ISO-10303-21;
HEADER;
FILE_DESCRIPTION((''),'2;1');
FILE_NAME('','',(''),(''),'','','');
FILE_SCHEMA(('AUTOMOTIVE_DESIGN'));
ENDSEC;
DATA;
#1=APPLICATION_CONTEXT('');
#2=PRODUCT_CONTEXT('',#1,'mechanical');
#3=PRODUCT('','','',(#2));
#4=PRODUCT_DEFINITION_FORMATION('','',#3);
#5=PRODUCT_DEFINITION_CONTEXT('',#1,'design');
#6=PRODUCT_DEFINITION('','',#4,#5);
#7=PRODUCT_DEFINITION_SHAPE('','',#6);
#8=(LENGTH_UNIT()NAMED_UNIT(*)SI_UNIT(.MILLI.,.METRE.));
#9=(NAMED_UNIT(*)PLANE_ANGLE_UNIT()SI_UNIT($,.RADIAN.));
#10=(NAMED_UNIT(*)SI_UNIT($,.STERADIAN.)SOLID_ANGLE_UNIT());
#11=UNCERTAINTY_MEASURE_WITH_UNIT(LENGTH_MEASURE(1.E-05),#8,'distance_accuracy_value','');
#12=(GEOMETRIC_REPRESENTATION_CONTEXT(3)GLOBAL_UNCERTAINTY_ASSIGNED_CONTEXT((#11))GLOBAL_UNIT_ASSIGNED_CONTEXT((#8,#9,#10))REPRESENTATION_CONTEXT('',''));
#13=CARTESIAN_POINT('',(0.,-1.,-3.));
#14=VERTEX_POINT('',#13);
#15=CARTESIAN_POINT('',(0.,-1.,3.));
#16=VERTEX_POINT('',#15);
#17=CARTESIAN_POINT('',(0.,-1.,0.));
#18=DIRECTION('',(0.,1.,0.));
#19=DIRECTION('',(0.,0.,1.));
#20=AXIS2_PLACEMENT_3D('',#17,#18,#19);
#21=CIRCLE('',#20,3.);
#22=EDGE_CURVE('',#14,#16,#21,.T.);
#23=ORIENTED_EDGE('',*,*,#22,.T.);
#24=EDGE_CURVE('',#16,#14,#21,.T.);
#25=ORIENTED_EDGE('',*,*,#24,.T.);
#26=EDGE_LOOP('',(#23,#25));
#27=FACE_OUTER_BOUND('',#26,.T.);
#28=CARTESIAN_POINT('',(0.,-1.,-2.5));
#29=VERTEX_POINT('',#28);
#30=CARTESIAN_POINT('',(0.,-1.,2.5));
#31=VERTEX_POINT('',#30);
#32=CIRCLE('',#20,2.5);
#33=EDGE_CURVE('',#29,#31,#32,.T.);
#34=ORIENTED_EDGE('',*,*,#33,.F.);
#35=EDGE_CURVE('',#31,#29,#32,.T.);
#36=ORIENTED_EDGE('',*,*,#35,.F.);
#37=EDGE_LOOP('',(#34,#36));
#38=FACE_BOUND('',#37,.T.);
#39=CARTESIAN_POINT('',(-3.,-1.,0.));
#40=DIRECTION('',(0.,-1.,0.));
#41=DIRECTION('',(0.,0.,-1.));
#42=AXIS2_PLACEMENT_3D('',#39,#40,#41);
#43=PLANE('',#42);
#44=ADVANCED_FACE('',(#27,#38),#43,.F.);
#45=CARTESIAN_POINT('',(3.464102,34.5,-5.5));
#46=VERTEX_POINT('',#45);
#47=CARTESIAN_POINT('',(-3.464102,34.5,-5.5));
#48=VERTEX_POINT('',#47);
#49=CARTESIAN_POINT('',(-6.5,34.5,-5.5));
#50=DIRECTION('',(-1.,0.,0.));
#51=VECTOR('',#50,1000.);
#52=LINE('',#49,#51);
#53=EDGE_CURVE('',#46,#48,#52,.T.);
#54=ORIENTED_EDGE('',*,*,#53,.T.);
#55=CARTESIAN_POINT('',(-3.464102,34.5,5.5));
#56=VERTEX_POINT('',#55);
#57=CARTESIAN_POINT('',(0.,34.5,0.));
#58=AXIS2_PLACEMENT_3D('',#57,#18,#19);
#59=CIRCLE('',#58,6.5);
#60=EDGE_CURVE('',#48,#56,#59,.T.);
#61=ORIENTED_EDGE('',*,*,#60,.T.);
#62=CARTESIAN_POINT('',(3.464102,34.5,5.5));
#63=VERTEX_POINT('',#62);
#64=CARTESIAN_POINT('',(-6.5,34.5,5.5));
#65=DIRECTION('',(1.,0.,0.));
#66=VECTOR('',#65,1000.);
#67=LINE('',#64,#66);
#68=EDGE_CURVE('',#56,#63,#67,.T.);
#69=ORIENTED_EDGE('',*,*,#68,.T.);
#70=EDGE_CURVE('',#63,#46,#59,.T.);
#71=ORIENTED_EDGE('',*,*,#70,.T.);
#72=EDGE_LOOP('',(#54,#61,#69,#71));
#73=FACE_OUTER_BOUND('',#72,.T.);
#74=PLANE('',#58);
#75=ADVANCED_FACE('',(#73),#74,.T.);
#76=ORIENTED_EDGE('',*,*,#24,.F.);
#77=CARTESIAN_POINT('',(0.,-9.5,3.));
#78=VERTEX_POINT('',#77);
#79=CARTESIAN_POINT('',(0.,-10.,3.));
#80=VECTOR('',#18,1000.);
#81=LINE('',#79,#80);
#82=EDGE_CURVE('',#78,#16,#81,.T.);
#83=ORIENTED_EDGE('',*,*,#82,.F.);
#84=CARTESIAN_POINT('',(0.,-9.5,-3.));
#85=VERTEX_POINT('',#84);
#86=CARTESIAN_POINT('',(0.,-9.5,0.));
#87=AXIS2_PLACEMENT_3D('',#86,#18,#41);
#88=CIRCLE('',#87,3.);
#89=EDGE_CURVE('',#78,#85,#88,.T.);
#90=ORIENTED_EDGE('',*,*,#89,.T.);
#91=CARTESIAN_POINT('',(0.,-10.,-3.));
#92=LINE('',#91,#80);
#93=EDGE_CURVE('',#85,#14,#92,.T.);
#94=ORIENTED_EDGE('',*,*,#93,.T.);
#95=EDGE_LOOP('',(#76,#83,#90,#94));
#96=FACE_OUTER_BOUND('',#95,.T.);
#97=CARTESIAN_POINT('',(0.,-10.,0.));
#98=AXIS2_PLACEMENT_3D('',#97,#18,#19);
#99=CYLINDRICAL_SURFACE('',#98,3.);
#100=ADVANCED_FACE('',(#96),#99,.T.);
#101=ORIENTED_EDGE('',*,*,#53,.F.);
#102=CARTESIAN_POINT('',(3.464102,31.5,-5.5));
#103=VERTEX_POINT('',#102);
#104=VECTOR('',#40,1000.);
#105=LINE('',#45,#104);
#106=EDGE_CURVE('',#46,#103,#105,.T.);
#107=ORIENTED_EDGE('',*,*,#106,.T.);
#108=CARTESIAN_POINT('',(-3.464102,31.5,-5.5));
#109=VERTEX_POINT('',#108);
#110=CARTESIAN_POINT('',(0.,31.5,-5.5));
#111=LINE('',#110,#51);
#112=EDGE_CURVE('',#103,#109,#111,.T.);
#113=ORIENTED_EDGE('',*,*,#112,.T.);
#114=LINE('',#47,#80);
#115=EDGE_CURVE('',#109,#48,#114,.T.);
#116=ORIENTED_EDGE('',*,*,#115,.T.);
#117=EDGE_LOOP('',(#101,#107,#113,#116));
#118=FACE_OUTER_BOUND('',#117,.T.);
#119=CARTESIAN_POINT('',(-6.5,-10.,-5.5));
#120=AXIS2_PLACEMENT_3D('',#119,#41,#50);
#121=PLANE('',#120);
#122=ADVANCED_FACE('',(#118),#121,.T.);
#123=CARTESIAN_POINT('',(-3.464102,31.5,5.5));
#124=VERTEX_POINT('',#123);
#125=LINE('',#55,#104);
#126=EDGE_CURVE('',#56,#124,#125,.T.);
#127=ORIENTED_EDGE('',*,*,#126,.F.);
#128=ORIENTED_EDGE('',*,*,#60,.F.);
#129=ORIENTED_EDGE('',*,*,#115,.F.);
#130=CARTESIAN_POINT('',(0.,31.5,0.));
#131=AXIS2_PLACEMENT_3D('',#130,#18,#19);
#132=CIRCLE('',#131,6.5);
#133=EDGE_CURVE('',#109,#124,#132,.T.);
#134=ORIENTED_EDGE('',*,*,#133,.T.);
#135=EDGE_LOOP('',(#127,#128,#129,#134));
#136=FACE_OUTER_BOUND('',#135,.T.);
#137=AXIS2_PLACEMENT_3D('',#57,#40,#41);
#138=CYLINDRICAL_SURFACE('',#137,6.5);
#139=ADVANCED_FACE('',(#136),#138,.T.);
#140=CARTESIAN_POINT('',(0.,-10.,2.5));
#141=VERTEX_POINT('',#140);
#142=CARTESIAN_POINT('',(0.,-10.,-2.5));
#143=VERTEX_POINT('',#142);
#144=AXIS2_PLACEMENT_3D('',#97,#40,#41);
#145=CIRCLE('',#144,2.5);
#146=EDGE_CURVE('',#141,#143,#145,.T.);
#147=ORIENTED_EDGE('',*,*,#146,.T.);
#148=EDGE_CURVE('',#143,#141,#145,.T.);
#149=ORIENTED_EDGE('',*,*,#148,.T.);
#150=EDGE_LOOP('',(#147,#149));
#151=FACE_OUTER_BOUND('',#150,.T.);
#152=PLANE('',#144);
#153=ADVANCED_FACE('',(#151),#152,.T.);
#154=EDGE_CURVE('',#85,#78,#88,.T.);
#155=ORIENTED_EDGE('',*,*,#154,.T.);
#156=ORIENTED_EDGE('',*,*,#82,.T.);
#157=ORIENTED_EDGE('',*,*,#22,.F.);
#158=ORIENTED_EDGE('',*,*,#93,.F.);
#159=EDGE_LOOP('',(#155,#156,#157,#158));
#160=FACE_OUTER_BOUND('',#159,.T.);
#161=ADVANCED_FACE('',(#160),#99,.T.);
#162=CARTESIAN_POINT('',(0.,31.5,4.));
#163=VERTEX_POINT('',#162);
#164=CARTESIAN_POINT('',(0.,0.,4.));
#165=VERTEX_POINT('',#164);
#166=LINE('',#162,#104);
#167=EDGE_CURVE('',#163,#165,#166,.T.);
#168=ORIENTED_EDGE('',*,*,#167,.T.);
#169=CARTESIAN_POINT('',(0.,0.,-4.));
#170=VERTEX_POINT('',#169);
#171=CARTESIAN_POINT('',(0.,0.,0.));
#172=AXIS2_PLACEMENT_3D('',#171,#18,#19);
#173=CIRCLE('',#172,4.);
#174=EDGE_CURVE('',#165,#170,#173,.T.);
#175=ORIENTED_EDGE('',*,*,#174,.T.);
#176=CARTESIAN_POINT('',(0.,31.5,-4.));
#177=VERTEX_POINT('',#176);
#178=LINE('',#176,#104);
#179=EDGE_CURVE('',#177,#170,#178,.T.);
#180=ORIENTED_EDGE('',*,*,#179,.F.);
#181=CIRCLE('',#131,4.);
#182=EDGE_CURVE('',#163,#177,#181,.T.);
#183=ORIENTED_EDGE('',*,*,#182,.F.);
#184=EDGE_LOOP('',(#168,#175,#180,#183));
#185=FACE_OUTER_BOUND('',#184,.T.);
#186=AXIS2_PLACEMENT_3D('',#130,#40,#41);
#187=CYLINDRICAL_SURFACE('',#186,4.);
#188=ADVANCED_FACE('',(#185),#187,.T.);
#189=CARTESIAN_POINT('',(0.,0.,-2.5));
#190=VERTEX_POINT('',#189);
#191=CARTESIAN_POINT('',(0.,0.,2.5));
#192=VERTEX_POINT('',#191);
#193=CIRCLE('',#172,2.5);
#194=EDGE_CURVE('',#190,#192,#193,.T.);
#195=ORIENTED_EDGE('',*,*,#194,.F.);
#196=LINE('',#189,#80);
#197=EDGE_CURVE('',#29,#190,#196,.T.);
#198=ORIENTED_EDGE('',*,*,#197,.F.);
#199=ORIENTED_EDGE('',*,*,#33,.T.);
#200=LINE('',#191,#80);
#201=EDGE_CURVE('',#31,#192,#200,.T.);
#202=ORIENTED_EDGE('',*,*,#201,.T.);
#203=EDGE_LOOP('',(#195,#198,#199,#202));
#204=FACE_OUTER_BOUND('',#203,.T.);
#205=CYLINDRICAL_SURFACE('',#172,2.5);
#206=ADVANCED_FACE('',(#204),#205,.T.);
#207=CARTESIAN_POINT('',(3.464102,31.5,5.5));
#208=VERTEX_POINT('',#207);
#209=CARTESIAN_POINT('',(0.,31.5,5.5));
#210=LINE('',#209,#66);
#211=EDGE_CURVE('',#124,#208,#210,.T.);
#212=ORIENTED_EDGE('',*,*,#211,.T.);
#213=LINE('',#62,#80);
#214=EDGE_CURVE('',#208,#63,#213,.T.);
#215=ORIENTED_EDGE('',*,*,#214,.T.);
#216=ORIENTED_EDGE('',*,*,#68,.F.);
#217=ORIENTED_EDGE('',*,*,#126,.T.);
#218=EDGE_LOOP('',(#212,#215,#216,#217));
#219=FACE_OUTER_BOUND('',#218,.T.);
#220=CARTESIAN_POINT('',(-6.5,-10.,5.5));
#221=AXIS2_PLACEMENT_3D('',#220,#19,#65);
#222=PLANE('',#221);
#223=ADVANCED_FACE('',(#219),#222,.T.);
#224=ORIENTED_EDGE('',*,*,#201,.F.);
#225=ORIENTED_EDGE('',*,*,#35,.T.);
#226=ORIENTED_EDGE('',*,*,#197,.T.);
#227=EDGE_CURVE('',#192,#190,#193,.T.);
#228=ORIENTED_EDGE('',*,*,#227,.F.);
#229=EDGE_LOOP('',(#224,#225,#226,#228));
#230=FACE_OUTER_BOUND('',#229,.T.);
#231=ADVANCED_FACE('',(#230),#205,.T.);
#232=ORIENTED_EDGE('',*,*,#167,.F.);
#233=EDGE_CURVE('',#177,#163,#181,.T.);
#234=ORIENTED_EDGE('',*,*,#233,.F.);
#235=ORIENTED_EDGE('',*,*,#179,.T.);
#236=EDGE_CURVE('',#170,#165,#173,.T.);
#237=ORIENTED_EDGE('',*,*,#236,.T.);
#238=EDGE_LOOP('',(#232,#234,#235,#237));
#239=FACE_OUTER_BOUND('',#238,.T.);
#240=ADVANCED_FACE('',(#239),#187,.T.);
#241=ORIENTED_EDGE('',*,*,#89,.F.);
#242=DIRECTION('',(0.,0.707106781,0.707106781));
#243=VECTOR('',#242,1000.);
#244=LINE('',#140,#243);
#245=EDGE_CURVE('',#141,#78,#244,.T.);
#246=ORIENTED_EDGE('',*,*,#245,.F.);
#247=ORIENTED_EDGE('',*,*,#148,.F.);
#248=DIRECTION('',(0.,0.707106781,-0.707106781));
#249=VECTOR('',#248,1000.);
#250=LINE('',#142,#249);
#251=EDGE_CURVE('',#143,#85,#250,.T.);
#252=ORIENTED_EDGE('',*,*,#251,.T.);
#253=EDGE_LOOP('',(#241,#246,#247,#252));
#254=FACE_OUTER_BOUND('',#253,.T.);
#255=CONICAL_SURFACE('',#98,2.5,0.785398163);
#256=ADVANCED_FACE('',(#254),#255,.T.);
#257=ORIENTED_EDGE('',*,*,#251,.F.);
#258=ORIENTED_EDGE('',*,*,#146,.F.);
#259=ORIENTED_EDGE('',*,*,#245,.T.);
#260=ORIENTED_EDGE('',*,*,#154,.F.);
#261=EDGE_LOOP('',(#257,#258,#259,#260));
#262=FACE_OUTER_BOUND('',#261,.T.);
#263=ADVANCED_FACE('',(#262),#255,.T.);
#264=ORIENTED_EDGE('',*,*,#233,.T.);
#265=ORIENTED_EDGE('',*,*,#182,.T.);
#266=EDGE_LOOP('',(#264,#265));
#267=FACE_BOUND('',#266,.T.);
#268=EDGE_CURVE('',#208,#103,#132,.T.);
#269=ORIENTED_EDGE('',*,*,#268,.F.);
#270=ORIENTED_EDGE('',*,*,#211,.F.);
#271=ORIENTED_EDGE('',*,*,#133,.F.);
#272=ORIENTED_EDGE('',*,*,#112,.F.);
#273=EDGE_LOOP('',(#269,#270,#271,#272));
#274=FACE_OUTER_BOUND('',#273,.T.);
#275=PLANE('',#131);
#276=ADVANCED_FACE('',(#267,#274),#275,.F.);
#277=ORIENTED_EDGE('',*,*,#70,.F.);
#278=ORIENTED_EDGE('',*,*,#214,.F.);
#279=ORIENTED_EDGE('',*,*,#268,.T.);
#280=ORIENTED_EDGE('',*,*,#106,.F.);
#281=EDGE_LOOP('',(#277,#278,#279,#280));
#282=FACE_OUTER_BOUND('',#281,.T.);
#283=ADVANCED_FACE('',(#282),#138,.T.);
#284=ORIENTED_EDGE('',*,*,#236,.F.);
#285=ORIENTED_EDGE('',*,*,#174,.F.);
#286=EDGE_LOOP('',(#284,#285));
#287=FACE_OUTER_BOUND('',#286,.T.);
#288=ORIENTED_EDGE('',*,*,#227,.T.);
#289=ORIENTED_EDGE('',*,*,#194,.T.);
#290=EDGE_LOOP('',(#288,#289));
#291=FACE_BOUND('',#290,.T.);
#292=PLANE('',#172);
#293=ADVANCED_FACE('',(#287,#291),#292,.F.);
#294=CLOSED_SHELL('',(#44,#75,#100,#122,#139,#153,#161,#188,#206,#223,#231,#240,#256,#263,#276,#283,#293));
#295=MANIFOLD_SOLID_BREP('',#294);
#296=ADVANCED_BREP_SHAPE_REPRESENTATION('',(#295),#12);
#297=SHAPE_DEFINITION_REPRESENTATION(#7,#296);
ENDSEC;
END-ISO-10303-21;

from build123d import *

# Parameters (mm, degrees)
SKETCH_1_R           = 4
EXTRUDE_1_DEPTH      = 31.5
SKETCH_2_R           = 3
EXTRUDE_2_DEPTH      = 10
SKETCH_3_R           = 6.5
EXTRUDE_3_DEPTH      = 3
SKETCH_4_OUTSIDE_W   = 24.63
SKETCH_4_OUTSIDE_H   = 24.63
SKETCH_4_OUTSIDE_W_2 = 13
SKETCH_4_OUTSIDE_H_2 = 11
CUT_EXTRUDE_1_DEPTH  = 46.439520244
CHAMFER_1_SIZE       = 0.5
SKETCH_5_W           = 0.5
SKETCH_5_H           = 1


with BuildPart() as part:
    # 草图1 → 凸台-拉伸1 (new body)
    with BuildSketch(Plane(origin=(0, 0, 0), x_dir=(1, 0, 0), z_dir=(0, 1, 0))):
        with Locations(Location((0, 0, 0), (0, 0, 270))):
            Circle(SKETCH_1_R)
    extrude(amount=EXTRUDE_1_DEPTH)

    # 草图2 → 凸台-拉伸2 (add)
    with BuildSketch(Plane.XZ):
        with Locations(Location((0, 0, 0), (0, 0, 270))):
            Circle(SKETCH_2_R)
    extrude(amount=EXTRUDE_2_DEPTH)

    # 草图3 → 凸台-拉伸3 (add)
    with BuildSketch(Plane(origin=(0, 31.5, 0), x_dir=(1, 0, 0), z_dir=(0, 1, 0))):
        with Locations(Location((0, 0, 0), (0, 0, 270))):
            Circle(SKETCH_3_R)
    extrude(amount=EXTRUDE_3_DEPTH)

    # 草图4 outside → 切除-拉伸1 (cut, through all)
    with BuildSketch(Plane(origin=(0, 34.5, 0), x_dir=(1, 0, 0), z_dir=(0, 1, 0))):
        Rectangle(SKETCH_4_OUTSIDE_W, SKETCH_4_OUTSIDE_H)
        Rectangle(SKETCH_4_OUTSIDE_W_2, SKETCH_4_OUTSIDE_H_2, mode=Mode.SUBTRACT)
    extrude(amount=-CUT_EXTRUDE_1_DEPTH, mode=Mode.SUBTRACT)

    # 倒角1
    chamfer_1_edges = [part.edges().sort_by_distance(p)[0] for p in [
        (0, -10, 3),
    ]]
    chamfer(chamfer_1_edges, length=CHAMFER_1_SIZE)

    # 草图5 → 切除-旋转1 (revolve, cut)
    with BuildSketch(Plane.XY, mode=Mode.PRIVATE) as cut_revolve_1_sk:
        with Locations((-2.75, -0.5)):
            Rectangle(SKETCH_5_W, SKETCH_5_H)
    revolve(cut_revolve_1_sk.sketch.rotate(Axis((0, 0, 0), (0, -1, 0)), 270), axis=Axis((0, 0, 0), (0, -1, 0)), mode=Mode.SUBTRACT)


solid = part.part
